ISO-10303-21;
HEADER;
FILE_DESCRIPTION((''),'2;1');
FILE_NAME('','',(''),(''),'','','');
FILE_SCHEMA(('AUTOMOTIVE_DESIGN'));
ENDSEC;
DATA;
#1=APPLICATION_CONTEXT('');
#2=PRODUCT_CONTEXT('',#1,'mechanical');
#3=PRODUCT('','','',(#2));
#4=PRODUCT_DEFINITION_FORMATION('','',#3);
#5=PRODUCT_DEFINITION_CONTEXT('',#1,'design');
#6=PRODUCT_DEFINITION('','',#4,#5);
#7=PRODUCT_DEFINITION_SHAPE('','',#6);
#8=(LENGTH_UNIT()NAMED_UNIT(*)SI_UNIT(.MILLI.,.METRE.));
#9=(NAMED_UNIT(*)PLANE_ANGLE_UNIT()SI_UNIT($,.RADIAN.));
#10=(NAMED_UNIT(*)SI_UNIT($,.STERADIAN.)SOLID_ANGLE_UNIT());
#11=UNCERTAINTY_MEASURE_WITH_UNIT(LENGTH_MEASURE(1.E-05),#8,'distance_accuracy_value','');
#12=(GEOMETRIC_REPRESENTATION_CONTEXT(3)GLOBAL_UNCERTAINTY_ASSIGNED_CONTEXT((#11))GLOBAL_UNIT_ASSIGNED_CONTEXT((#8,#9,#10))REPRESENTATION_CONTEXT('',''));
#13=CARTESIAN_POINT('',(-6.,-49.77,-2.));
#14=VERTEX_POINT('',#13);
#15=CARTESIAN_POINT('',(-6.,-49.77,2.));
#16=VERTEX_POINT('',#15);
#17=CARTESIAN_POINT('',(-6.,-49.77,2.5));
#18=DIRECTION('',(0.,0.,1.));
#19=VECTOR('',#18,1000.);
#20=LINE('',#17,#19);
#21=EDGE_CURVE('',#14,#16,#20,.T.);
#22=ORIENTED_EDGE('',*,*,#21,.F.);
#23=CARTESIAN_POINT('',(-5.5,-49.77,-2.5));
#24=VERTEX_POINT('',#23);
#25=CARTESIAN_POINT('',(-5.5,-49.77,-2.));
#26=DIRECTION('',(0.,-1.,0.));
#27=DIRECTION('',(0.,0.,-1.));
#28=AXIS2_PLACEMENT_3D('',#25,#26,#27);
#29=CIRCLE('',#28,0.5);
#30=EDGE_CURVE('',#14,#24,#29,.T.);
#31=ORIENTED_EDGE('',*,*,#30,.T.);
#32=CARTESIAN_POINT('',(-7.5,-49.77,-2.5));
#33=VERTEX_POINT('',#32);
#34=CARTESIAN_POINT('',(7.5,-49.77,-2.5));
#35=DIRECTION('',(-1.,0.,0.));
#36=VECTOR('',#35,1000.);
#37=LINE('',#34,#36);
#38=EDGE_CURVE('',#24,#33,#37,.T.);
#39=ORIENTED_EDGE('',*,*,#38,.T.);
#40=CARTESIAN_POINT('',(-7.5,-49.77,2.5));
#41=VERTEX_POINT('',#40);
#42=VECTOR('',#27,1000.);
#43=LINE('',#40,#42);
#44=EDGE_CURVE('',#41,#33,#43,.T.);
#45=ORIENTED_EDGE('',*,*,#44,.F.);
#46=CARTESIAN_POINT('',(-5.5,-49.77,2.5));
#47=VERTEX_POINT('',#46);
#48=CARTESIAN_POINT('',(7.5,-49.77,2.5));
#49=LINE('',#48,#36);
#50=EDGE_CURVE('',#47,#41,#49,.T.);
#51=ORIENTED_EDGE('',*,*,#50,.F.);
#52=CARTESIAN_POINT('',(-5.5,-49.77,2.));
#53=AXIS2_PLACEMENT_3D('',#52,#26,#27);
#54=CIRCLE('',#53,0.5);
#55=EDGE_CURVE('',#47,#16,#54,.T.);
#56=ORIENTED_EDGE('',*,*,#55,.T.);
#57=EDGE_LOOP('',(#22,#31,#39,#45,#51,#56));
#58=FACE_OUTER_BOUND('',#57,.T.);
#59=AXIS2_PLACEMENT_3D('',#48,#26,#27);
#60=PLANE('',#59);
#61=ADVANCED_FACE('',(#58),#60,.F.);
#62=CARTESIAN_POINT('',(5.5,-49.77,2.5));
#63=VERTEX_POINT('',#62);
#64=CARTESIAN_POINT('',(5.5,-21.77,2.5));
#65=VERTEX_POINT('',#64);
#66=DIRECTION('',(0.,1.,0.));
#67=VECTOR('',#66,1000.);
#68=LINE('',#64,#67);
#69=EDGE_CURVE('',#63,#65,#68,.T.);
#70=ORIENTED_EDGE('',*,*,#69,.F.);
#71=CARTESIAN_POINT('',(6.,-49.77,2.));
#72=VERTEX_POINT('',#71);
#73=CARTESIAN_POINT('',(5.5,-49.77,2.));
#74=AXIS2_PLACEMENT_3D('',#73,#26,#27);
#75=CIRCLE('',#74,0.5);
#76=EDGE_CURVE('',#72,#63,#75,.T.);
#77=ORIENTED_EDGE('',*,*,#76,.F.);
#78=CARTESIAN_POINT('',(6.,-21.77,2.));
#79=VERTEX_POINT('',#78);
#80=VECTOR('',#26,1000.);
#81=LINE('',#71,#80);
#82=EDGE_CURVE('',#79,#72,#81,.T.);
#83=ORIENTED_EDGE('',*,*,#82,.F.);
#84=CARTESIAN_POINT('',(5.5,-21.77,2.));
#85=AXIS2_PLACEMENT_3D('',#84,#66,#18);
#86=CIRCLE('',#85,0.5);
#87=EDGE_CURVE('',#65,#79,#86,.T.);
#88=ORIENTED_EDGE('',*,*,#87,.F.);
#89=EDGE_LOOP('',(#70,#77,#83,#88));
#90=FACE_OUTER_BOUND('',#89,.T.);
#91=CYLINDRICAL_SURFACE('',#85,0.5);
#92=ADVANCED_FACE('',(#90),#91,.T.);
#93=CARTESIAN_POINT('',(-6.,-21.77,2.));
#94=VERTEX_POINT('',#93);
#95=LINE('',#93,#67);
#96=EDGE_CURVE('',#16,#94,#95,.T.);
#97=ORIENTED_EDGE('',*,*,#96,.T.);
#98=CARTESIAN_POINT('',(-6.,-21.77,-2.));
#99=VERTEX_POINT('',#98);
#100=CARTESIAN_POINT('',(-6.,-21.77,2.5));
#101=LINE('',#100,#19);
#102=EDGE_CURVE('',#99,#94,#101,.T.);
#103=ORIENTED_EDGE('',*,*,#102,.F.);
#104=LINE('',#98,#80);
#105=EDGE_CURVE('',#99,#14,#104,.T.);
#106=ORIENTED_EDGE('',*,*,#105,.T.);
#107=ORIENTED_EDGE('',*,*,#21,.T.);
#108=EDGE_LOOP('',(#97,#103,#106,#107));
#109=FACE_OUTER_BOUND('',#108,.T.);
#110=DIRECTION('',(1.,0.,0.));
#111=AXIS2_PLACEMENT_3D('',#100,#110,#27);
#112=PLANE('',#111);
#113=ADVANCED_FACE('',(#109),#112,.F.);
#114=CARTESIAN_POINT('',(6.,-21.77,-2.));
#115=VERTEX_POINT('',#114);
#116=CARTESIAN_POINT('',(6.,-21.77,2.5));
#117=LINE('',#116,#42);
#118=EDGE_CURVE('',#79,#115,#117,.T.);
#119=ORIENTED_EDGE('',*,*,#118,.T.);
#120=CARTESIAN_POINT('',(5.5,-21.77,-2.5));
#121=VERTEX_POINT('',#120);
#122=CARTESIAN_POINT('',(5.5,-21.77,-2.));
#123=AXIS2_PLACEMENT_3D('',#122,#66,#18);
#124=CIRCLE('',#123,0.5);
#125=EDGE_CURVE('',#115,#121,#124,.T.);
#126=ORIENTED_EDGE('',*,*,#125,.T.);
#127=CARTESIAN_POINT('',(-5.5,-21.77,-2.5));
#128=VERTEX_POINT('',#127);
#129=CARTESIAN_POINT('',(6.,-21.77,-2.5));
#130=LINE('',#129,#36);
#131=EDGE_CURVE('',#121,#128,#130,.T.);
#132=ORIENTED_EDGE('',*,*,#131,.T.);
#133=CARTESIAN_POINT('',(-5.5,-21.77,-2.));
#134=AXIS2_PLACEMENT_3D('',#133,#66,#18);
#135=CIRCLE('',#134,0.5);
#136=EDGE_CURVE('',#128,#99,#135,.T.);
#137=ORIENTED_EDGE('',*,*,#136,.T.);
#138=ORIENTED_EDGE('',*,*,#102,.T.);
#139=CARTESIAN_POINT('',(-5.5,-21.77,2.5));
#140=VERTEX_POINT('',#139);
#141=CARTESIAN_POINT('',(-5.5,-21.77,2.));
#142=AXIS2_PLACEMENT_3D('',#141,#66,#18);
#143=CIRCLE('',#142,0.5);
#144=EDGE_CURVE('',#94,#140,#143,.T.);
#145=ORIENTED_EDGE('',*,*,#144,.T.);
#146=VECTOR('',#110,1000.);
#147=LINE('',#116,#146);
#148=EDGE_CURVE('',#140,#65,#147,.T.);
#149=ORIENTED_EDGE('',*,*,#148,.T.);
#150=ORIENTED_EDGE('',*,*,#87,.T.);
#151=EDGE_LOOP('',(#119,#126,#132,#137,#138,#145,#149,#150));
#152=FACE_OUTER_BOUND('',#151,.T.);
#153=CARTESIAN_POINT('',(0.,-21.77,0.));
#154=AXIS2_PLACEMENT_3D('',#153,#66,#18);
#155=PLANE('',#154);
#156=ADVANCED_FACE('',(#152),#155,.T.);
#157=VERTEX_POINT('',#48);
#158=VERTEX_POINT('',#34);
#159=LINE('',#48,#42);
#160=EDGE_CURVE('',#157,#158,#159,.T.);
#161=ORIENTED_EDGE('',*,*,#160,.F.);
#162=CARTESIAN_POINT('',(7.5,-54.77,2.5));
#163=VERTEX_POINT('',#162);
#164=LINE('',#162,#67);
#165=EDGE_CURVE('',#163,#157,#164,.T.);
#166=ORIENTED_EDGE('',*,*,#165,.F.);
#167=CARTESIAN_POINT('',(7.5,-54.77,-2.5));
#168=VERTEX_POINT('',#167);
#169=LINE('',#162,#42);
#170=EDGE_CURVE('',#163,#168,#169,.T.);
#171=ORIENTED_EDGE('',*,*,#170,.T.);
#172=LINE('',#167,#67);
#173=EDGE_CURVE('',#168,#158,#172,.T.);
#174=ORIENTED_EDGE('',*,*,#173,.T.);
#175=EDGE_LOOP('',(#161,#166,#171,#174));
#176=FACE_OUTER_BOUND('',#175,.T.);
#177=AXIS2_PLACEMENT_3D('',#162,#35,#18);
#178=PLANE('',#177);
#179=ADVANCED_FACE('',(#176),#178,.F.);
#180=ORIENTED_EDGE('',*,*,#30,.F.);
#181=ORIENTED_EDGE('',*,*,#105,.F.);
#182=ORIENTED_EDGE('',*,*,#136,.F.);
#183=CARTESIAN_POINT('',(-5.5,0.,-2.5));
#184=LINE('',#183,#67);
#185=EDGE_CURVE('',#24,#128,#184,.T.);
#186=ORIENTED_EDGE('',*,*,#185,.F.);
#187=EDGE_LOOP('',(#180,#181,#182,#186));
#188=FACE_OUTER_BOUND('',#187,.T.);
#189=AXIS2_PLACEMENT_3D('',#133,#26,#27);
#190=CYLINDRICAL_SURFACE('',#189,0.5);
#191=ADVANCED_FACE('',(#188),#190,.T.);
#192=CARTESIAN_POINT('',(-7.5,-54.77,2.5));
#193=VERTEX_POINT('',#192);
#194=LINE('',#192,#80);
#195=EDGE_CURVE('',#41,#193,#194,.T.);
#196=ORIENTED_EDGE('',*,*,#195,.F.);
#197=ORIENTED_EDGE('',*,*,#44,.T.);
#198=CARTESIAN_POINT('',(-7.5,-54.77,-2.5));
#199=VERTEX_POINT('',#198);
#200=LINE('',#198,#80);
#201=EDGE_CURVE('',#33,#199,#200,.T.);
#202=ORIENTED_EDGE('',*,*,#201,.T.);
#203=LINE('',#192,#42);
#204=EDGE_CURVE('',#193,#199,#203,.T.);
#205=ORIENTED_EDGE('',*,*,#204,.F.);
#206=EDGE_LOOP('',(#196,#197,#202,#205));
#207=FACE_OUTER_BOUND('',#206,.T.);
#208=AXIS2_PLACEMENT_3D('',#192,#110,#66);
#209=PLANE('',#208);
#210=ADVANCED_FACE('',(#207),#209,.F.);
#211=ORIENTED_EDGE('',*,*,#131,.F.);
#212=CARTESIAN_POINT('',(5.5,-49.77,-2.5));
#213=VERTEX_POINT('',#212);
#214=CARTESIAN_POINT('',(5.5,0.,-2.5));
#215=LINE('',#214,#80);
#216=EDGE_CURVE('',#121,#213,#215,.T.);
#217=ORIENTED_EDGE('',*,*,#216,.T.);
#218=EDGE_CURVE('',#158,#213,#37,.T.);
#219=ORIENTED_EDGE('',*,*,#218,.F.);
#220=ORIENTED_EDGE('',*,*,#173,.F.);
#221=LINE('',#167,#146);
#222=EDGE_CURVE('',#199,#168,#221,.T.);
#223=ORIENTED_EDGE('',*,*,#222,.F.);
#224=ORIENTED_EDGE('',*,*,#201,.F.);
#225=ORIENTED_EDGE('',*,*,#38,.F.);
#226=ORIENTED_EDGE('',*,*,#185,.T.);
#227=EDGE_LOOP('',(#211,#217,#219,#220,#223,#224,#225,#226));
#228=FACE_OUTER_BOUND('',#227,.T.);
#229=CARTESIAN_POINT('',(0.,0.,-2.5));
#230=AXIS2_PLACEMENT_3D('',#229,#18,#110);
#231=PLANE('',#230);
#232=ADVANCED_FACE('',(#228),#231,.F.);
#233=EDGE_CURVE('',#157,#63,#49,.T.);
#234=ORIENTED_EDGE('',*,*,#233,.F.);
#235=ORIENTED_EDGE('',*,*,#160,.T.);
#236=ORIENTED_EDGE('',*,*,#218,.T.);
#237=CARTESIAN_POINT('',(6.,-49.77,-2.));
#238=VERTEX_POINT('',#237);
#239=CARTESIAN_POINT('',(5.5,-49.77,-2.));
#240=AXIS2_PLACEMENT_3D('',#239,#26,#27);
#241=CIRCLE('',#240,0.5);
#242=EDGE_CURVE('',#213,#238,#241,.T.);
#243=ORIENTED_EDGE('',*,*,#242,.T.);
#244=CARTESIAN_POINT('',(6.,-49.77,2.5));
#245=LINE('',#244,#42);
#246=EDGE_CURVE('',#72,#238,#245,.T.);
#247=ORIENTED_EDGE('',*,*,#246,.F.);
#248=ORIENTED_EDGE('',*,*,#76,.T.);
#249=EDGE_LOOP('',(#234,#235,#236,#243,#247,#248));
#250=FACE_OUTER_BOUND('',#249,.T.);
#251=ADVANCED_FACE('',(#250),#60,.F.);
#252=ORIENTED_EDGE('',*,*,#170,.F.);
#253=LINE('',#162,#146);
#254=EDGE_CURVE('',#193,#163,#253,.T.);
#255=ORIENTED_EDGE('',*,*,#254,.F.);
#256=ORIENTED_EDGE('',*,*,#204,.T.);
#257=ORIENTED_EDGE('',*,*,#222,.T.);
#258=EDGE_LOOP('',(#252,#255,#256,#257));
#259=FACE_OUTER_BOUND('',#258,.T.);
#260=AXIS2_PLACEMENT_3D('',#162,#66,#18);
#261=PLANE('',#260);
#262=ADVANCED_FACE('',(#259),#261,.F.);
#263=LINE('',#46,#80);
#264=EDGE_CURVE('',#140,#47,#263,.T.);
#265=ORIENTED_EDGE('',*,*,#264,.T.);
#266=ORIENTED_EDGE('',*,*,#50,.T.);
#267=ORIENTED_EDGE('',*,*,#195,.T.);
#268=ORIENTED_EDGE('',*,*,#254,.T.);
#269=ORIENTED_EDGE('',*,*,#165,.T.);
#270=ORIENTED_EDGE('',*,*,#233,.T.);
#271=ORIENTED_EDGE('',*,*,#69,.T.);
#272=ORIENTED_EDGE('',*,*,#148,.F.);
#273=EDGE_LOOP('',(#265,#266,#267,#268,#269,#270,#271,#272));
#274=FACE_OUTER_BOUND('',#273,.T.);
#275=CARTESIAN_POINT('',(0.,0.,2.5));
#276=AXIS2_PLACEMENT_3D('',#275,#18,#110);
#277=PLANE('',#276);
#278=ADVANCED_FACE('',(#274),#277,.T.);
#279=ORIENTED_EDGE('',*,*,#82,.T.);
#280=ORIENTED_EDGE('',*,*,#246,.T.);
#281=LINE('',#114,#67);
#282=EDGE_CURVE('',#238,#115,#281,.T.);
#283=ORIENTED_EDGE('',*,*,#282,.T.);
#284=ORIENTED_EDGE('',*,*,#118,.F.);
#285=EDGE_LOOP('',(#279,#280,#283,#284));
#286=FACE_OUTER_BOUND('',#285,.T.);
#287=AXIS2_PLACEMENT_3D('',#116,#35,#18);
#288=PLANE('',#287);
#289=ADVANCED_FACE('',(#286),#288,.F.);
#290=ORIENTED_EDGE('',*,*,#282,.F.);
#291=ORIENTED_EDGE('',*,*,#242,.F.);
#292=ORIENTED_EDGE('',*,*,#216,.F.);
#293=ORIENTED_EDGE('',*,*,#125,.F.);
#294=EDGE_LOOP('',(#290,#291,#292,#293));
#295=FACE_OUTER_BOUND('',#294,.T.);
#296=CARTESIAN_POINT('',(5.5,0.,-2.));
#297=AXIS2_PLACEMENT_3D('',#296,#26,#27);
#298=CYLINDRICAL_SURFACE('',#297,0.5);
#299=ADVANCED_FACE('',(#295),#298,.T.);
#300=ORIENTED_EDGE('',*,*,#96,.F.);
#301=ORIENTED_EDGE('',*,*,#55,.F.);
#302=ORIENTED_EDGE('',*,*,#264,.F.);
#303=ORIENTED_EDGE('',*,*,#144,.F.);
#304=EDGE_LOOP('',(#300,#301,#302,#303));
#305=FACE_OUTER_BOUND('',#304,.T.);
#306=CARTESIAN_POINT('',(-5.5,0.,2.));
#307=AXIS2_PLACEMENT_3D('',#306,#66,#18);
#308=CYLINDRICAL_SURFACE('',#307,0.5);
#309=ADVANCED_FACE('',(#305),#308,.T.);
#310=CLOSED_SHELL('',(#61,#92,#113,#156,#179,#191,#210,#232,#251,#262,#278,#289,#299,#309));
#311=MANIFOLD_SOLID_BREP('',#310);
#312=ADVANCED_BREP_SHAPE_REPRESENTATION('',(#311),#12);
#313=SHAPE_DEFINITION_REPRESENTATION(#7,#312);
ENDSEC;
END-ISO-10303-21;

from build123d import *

# Parameters (mm, degrees)
SKETCH1_W           = 15
SKETCH1_H           = 5
BOSS_EXTRUDE1_DEPTH = 2.5
SKETCH3_W           = 12
SKETCH3_H           = 5
BOSS_EXTRUDE2_DEPTH = 28
FILLET1_R           = 0.5


with BuildPart() as part:
    # Sketch1 → Boss-Extrude1 (new, symmetric)
    with BuildSketch(Plane.XY):
        with Locations((0, -52.27)):
            Rectangle(SKETCH1_W, SKETCH1_H)
    extrude(amount=BOSS_EXTRUDE1_DEPTH, both=True)

    # Sketch3 → Boss-Extrude2 (add)
    with BuildSketch(Plane(origin=(0, -49.77, 0), x_dir=(1, 0, 0), z_dir=(0, 1, 0))):
        Rectangle(SKETCH3_W, SKETCH3_H)
    extrude(amount=BOSS_EXTRUDE2_DEPTH)

    # Fillet1
    fillet1_edges = [part.edges().sort_by_distance(p)[0] for p in [
        (-6, -35.77, -2.5),
        (-6, -35.77, 2.5),
        (6, -35.77, 2.5),
        (6, -35.77, -2.5),
    ]]
    fillet(fillet1_edges, radius=FILLET1_R)


solid = part.part
